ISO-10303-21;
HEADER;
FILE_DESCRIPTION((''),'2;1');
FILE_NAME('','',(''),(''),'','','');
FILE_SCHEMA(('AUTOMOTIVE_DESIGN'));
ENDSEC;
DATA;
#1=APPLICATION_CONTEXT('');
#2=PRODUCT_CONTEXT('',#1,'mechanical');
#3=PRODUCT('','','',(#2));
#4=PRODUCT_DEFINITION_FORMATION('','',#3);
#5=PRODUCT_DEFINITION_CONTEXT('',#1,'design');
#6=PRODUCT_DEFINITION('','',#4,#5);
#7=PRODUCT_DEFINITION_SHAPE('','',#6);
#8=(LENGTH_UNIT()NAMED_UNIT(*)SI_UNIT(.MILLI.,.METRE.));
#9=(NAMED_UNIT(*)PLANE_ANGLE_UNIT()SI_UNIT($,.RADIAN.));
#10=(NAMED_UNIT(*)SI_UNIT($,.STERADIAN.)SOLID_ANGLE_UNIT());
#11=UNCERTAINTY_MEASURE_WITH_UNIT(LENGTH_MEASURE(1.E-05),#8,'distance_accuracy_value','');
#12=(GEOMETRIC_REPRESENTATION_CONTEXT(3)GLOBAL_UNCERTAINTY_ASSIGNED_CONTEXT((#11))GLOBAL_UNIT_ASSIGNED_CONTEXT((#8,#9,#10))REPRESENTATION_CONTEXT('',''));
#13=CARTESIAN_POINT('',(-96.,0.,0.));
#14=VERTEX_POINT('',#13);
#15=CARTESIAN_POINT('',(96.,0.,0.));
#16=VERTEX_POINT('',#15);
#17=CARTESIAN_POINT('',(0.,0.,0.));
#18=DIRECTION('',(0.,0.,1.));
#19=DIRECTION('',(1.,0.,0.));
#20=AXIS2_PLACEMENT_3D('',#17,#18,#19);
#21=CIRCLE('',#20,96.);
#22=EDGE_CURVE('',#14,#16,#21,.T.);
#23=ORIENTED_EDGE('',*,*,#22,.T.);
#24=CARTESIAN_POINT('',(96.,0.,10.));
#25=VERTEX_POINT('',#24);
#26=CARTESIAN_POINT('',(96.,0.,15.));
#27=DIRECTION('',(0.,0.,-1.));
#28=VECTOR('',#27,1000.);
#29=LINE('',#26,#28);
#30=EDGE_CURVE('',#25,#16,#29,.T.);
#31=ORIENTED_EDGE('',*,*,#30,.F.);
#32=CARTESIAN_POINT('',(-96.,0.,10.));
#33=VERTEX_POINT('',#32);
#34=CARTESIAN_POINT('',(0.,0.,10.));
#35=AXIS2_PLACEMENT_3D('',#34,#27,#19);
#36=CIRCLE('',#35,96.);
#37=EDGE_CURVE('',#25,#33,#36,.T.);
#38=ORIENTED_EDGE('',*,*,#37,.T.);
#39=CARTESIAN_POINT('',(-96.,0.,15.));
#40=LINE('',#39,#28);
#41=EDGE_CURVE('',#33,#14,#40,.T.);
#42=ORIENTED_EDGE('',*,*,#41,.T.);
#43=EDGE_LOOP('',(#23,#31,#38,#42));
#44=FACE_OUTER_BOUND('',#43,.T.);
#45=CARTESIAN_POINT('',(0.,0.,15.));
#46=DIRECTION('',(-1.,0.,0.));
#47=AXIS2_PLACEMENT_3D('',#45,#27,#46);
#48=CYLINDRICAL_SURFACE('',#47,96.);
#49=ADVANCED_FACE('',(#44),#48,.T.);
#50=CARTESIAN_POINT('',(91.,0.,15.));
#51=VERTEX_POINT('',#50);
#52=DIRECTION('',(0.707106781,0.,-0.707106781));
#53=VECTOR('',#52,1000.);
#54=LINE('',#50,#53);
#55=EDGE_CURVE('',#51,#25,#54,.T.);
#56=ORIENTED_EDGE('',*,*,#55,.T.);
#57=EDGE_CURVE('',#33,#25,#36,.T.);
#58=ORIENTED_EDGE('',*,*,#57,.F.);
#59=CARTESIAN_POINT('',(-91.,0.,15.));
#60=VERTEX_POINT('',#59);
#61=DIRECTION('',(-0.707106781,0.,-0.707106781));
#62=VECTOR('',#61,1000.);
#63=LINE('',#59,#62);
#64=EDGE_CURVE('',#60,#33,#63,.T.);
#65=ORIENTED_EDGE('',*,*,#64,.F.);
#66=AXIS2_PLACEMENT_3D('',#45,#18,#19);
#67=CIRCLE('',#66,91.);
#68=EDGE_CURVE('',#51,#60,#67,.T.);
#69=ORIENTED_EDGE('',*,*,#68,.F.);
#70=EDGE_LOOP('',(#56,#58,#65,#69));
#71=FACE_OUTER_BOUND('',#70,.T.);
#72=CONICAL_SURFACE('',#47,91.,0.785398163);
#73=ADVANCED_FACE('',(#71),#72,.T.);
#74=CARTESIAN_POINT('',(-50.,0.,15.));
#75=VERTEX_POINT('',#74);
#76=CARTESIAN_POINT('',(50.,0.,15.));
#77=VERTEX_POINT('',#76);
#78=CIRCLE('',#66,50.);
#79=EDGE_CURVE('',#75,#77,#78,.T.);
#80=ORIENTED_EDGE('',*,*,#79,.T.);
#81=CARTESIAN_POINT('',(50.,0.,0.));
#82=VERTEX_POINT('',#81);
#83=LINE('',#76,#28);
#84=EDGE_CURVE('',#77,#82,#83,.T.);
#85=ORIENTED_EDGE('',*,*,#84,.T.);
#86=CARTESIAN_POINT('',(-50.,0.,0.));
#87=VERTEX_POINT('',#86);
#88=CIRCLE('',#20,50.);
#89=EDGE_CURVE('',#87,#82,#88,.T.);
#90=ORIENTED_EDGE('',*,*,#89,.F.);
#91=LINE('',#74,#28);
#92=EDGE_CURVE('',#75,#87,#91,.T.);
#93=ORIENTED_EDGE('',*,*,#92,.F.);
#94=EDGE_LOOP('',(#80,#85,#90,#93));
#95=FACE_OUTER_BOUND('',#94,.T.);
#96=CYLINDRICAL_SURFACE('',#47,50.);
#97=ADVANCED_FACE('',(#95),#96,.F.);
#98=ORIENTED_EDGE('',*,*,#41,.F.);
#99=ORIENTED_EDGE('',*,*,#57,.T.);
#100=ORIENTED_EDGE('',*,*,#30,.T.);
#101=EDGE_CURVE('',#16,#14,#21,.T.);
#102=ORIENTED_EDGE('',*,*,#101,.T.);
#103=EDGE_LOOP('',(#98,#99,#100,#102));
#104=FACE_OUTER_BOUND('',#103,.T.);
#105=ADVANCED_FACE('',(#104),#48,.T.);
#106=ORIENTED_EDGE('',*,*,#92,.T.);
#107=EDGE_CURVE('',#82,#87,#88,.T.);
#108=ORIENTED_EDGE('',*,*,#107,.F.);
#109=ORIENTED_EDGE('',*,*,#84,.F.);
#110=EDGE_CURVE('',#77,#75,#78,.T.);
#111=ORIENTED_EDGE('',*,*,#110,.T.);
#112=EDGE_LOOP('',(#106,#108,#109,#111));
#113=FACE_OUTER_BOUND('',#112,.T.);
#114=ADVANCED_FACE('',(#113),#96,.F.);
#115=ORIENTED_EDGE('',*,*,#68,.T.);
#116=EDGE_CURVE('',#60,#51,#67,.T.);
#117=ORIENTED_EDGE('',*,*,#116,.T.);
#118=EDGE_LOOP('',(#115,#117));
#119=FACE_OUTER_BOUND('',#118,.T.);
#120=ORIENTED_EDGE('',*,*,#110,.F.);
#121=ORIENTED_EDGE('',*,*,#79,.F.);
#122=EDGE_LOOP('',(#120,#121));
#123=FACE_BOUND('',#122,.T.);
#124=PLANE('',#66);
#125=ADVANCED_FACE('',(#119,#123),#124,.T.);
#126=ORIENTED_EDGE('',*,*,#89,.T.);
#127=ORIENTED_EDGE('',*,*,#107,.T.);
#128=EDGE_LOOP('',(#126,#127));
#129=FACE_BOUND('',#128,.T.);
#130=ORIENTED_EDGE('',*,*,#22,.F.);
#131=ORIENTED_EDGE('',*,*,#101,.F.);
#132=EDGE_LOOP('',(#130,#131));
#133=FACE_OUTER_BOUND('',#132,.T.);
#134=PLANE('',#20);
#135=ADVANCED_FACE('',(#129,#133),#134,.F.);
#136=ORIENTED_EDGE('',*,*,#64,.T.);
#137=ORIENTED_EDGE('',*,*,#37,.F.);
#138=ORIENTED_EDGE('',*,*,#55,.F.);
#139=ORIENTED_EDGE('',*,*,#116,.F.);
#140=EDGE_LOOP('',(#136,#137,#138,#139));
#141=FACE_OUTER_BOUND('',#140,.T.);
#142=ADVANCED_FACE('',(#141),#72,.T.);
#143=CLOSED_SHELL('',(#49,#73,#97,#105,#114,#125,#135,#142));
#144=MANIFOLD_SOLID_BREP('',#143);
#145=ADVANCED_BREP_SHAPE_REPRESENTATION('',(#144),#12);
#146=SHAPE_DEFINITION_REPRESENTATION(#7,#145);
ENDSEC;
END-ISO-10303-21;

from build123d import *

# Parameters (mm, degrees)
SKETCH1_R           = 96
SKETCH1_R_2         = 50
BOSS_EXTRUDE1_DEPTH = 15
CHAMFER1_SIZE       = 5


with BuildPart() as part:
    # Sketch1 → Boss-Extrude1 (new body)
    with BuildSketch(Plane.XY):
        Circle(SKETCH1_R)
        Circle(SKETCH1_R_2, mode=Mode.SUBTRACT)
    extrude(amount=BOSS_EXTRUDE1_DEPTH)

    # Chamfer1
    chamfer1_edges = [part.edges().sort_by_distance(p)[0] for p in [
        (-96, 0, 15),
    ]]
    chamfer(chamfer1_edges, length=CHAMFER1_SIZE)


solid = part.part
